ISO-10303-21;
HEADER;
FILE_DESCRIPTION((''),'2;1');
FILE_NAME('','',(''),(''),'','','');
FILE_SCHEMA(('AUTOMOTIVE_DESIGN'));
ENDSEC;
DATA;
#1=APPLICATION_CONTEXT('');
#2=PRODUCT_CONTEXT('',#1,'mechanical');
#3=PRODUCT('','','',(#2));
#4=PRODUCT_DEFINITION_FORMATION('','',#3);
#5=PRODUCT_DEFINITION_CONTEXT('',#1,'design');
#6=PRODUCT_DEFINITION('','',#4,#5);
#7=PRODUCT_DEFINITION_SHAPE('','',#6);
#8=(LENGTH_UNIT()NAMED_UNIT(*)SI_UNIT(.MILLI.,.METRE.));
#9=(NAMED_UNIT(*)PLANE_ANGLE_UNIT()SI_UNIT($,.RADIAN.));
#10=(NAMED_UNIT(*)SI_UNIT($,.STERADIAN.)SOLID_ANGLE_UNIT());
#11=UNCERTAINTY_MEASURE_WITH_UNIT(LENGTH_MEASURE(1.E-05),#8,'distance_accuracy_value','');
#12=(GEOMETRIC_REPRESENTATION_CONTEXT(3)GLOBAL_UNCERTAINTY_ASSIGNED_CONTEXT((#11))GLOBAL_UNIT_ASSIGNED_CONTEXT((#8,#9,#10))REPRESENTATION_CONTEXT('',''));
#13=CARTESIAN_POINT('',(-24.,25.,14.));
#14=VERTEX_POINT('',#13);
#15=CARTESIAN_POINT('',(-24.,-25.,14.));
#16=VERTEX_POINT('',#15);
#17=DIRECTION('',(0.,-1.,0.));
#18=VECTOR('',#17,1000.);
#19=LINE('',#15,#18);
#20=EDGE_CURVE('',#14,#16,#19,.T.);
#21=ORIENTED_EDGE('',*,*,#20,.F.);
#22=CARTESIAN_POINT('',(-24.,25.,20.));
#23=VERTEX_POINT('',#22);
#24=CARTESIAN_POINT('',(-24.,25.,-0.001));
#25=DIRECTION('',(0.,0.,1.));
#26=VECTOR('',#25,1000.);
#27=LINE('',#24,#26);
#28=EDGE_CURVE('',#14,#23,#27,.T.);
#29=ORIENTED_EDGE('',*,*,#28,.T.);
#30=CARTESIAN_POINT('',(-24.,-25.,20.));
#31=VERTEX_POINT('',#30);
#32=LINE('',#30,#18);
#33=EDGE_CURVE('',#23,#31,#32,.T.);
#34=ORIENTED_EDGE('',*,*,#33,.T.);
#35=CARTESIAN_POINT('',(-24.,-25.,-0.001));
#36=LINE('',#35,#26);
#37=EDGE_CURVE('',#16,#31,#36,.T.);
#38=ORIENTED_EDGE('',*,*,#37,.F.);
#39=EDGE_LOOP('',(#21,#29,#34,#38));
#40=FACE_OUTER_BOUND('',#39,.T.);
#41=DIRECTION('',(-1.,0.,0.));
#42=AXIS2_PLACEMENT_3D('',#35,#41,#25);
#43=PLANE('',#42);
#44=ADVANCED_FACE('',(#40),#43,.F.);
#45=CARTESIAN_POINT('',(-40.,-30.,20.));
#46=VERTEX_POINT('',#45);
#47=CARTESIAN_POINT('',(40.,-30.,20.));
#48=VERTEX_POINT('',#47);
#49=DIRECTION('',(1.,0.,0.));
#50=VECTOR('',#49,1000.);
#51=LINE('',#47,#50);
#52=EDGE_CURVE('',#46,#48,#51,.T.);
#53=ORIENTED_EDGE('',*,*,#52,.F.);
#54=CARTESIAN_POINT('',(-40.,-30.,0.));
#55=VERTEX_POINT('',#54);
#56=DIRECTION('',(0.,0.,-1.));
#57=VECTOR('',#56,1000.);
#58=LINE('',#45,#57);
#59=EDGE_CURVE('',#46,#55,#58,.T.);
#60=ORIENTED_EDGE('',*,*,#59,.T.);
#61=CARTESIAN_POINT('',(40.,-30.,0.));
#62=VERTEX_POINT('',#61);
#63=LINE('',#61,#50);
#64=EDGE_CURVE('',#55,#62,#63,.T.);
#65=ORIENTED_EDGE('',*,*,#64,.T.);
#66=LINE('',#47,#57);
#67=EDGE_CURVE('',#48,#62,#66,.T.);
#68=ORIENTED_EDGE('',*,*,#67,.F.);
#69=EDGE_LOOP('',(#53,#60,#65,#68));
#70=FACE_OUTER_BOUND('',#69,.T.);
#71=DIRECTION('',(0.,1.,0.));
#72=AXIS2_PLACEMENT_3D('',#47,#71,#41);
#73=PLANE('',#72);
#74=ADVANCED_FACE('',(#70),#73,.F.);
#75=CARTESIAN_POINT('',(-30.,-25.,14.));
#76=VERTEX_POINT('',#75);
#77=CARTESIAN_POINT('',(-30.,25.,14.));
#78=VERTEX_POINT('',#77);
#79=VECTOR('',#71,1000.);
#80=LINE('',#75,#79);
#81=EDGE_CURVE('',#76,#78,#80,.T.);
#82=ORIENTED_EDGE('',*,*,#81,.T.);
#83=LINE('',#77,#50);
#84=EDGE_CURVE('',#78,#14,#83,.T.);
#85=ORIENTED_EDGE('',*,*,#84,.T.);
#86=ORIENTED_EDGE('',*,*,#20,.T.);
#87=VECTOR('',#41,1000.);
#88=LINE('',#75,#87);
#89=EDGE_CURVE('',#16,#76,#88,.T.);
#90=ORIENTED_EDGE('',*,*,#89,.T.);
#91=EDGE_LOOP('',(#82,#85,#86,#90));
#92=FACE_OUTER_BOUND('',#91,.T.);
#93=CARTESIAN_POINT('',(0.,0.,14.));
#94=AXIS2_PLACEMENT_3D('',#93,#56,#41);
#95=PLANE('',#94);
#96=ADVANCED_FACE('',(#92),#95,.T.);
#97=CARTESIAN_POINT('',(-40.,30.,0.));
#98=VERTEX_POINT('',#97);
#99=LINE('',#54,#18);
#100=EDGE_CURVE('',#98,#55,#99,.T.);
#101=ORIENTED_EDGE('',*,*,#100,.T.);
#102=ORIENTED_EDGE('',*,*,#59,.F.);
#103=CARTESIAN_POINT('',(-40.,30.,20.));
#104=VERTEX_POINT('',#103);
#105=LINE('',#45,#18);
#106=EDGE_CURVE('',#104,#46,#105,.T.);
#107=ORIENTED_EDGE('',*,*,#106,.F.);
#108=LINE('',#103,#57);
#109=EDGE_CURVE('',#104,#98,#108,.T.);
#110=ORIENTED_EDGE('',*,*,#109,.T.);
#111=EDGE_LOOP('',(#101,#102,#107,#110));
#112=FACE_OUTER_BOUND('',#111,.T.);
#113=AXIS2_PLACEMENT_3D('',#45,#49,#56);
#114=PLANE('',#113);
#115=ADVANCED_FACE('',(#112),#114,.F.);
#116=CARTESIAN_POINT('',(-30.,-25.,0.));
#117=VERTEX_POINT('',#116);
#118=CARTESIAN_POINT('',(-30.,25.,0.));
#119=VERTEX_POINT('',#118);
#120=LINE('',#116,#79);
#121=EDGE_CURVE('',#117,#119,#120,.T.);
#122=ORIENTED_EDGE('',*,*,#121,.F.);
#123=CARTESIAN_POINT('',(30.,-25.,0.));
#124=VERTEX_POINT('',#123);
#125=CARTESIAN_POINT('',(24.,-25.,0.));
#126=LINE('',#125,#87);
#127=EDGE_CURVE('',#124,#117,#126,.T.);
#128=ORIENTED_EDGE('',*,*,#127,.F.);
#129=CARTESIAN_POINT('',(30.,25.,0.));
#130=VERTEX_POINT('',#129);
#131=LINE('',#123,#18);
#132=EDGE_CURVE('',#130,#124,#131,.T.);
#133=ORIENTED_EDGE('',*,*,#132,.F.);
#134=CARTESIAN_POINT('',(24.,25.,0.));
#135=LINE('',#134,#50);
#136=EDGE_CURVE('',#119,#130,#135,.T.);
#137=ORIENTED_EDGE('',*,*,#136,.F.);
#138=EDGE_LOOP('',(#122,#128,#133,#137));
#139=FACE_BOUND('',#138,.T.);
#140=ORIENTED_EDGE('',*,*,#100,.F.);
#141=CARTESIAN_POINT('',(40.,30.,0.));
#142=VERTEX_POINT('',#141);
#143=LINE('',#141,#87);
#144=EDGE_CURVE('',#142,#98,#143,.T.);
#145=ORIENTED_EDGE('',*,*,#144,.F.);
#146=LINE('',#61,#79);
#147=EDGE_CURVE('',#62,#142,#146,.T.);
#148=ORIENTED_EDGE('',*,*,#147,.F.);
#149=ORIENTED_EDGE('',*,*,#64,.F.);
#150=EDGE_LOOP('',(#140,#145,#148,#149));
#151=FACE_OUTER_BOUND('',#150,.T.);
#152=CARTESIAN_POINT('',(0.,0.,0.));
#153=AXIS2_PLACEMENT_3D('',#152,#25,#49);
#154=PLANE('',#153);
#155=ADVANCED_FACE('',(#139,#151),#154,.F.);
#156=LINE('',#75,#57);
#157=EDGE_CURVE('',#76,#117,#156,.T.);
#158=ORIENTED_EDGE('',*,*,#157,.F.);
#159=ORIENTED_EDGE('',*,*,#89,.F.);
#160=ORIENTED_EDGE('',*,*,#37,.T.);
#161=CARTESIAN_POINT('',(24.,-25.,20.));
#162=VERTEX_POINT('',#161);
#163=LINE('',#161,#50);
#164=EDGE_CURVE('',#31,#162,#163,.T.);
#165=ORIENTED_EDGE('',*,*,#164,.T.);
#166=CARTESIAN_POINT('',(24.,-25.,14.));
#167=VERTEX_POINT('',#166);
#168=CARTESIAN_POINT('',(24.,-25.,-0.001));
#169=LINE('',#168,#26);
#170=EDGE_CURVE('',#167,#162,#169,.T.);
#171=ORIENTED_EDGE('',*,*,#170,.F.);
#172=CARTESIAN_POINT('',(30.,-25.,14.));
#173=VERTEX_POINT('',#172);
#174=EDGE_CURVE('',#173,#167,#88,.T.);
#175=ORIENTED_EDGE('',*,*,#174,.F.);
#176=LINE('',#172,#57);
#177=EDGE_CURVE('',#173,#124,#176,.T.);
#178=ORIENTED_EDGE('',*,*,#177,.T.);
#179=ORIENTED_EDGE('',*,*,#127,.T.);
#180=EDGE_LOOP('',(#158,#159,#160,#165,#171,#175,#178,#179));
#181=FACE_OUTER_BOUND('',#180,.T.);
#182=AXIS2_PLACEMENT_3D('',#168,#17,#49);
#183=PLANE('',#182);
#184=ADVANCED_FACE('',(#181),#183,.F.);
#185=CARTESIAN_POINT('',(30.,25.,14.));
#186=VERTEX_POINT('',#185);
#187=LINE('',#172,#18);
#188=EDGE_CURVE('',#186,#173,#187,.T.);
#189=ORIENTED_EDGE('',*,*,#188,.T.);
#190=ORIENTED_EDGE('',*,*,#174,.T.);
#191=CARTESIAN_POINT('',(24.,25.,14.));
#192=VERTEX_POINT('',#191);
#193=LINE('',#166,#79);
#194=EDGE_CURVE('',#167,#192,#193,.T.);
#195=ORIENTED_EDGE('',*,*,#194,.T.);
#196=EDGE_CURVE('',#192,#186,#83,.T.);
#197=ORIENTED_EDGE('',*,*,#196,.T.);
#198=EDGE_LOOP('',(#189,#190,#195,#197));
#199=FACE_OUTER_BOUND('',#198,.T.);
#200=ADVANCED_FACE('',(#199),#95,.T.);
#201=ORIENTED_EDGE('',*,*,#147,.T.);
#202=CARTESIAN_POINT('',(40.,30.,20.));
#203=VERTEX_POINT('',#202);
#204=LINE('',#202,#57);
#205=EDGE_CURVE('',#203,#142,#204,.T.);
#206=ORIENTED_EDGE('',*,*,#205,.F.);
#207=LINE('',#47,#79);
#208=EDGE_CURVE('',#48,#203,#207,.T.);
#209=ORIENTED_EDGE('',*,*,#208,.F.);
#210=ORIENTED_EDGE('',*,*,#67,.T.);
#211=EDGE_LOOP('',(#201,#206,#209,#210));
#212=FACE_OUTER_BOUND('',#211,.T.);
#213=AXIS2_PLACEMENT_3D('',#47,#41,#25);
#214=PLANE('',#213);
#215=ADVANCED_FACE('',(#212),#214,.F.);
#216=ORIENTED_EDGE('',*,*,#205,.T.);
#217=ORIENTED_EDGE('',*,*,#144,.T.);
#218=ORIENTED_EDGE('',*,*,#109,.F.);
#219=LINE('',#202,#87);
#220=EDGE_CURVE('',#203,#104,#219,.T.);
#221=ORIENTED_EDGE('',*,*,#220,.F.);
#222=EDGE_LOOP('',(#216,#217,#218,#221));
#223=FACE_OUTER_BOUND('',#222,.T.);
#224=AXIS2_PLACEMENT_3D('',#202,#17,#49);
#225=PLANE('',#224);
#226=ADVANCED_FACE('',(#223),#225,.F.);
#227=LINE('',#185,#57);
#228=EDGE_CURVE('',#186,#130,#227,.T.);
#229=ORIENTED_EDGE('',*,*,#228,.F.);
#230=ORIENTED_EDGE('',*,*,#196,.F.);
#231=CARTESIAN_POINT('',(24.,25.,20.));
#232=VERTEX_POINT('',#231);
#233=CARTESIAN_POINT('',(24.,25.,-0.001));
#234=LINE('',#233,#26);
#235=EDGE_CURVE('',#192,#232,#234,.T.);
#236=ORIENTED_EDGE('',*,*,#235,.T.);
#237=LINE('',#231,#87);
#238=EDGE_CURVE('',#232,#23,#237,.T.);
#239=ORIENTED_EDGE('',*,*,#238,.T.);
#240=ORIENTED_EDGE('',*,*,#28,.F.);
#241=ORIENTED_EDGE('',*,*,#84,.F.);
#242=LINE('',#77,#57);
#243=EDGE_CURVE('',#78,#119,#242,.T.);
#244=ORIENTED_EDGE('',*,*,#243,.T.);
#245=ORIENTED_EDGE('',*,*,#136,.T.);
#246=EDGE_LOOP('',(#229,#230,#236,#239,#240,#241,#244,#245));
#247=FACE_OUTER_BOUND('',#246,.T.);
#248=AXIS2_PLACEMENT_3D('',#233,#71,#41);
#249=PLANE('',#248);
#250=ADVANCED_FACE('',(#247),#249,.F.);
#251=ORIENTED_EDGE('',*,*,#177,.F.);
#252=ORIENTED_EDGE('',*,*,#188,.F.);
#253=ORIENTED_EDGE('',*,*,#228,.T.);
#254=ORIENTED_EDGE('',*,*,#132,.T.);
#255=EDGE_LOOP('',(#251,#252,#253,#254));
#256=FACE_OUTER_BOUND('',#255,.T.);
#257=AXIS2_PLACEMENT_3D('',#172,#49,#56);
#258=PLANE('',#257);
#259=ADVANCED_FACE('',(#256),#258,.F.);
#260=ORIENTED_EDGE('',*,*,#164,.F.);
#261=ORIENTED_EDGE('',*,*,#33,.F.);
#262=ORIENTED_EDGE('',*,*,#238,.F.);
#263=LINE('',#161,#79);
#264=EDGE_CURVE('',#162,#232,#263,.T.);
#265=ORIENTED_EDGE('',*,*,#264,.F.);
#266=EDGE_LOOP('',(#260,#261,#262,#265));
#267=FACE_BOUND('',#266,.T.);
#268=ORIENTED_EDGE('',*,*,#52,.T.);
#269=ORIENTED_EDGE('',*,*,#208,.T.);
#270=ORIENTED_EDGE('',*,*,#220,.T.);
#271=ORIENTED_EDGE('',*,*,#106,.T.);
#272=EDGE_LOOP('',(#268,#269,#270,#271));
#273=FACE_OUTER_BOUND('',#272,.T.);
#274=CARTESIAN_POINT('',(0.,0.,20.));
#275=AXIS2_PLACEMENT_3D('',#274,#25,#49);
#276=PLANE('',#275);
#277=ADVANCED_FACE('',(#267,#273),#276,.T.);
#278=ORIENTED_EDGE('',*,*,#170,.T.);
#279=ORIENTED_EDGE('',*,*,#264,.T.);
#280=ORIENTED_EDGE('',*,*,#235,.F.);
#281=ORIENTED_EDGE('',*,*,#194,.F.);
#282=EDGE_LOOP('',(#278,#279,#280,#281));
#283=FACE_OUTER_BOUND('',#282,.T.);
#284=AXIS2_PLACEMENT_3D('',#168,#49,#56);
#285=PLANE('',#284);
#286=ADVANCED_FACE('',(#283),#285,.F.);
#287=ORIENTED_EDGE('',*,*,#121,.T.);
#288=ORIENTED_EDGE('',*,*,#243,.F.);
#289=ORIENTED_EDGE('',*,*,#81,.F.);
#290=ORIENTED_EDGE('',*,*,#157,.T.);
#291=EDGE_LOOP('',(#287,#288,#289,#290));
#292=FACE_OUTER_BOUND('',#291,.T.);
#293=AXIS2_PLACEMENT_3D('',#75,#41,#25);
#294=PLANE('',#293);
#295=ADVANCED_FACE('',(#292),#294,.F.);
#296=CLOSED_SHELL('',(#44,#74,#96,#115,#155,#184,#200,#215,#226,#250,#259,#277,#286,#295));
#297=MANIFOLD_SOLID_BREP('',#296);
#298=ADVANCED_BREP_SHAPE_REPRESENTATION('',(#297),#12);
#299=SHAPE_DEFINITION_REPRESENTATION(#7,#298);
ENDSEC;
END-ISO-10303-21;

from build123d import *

# Parameters (mm, degrees)
SKETCH_1_W          = 80
SKETCH_1_H          = 60
EXTRUDE_1_DEPTH     = 20
CUT_EXTRUDE_1_REACH = 55.852
SKETCH_2_W          = 48
SKETCH_2_H          = 50
SKETCH_3_W          = 60
SKETCH_3_H          = 50
CUT_EXTRUDE_2_DEPTH = 14


with BuildPart() as part:
    # 草图1 → 凸台-拉伸1 (new body)
    with BuildSketch(Plane.XY):
        Rectangle(SKETCH_1_W, SKETCH_1_H)
    extrude(amount=EXTRUDE_1_DEPTH)

    # 草图2 → 切除-拉伸1 (cut, up to next)
    with BuildSketch(Plane.XY.offset(20), mode=Mode.PRIVATE) as cut_extrude_1_sk1:
        Rectangle(SKETCH_2_W, SKETCH_2_H)
    cut_extrude_1_tool1 = extrude(cut_extrude_1_sk1.sketch, amount=-CUT_EXTRUDE_1_REACH, mode=Mode.PRIVATE) & part.part
    add(cut_extrude_1_tool1.solids().sort_by_distance((0, 0, 20))[0], mode=Mode.SUBTRACT)

    # 草图3 → 切除-拉伸2 (cut)
    with BuildSketch(Plane(origin=(0, 0, 0), x_dir=(-1, 0, 0), z_dir=(0, 0, -1))):
        Rectangle(SKETCH_3_W, SKETCH_3_H)
    extrude(amount=-CUT_EXTRUDE_2_DEPTH, mode=Mode.SUBTRACT)


solid = part.part
